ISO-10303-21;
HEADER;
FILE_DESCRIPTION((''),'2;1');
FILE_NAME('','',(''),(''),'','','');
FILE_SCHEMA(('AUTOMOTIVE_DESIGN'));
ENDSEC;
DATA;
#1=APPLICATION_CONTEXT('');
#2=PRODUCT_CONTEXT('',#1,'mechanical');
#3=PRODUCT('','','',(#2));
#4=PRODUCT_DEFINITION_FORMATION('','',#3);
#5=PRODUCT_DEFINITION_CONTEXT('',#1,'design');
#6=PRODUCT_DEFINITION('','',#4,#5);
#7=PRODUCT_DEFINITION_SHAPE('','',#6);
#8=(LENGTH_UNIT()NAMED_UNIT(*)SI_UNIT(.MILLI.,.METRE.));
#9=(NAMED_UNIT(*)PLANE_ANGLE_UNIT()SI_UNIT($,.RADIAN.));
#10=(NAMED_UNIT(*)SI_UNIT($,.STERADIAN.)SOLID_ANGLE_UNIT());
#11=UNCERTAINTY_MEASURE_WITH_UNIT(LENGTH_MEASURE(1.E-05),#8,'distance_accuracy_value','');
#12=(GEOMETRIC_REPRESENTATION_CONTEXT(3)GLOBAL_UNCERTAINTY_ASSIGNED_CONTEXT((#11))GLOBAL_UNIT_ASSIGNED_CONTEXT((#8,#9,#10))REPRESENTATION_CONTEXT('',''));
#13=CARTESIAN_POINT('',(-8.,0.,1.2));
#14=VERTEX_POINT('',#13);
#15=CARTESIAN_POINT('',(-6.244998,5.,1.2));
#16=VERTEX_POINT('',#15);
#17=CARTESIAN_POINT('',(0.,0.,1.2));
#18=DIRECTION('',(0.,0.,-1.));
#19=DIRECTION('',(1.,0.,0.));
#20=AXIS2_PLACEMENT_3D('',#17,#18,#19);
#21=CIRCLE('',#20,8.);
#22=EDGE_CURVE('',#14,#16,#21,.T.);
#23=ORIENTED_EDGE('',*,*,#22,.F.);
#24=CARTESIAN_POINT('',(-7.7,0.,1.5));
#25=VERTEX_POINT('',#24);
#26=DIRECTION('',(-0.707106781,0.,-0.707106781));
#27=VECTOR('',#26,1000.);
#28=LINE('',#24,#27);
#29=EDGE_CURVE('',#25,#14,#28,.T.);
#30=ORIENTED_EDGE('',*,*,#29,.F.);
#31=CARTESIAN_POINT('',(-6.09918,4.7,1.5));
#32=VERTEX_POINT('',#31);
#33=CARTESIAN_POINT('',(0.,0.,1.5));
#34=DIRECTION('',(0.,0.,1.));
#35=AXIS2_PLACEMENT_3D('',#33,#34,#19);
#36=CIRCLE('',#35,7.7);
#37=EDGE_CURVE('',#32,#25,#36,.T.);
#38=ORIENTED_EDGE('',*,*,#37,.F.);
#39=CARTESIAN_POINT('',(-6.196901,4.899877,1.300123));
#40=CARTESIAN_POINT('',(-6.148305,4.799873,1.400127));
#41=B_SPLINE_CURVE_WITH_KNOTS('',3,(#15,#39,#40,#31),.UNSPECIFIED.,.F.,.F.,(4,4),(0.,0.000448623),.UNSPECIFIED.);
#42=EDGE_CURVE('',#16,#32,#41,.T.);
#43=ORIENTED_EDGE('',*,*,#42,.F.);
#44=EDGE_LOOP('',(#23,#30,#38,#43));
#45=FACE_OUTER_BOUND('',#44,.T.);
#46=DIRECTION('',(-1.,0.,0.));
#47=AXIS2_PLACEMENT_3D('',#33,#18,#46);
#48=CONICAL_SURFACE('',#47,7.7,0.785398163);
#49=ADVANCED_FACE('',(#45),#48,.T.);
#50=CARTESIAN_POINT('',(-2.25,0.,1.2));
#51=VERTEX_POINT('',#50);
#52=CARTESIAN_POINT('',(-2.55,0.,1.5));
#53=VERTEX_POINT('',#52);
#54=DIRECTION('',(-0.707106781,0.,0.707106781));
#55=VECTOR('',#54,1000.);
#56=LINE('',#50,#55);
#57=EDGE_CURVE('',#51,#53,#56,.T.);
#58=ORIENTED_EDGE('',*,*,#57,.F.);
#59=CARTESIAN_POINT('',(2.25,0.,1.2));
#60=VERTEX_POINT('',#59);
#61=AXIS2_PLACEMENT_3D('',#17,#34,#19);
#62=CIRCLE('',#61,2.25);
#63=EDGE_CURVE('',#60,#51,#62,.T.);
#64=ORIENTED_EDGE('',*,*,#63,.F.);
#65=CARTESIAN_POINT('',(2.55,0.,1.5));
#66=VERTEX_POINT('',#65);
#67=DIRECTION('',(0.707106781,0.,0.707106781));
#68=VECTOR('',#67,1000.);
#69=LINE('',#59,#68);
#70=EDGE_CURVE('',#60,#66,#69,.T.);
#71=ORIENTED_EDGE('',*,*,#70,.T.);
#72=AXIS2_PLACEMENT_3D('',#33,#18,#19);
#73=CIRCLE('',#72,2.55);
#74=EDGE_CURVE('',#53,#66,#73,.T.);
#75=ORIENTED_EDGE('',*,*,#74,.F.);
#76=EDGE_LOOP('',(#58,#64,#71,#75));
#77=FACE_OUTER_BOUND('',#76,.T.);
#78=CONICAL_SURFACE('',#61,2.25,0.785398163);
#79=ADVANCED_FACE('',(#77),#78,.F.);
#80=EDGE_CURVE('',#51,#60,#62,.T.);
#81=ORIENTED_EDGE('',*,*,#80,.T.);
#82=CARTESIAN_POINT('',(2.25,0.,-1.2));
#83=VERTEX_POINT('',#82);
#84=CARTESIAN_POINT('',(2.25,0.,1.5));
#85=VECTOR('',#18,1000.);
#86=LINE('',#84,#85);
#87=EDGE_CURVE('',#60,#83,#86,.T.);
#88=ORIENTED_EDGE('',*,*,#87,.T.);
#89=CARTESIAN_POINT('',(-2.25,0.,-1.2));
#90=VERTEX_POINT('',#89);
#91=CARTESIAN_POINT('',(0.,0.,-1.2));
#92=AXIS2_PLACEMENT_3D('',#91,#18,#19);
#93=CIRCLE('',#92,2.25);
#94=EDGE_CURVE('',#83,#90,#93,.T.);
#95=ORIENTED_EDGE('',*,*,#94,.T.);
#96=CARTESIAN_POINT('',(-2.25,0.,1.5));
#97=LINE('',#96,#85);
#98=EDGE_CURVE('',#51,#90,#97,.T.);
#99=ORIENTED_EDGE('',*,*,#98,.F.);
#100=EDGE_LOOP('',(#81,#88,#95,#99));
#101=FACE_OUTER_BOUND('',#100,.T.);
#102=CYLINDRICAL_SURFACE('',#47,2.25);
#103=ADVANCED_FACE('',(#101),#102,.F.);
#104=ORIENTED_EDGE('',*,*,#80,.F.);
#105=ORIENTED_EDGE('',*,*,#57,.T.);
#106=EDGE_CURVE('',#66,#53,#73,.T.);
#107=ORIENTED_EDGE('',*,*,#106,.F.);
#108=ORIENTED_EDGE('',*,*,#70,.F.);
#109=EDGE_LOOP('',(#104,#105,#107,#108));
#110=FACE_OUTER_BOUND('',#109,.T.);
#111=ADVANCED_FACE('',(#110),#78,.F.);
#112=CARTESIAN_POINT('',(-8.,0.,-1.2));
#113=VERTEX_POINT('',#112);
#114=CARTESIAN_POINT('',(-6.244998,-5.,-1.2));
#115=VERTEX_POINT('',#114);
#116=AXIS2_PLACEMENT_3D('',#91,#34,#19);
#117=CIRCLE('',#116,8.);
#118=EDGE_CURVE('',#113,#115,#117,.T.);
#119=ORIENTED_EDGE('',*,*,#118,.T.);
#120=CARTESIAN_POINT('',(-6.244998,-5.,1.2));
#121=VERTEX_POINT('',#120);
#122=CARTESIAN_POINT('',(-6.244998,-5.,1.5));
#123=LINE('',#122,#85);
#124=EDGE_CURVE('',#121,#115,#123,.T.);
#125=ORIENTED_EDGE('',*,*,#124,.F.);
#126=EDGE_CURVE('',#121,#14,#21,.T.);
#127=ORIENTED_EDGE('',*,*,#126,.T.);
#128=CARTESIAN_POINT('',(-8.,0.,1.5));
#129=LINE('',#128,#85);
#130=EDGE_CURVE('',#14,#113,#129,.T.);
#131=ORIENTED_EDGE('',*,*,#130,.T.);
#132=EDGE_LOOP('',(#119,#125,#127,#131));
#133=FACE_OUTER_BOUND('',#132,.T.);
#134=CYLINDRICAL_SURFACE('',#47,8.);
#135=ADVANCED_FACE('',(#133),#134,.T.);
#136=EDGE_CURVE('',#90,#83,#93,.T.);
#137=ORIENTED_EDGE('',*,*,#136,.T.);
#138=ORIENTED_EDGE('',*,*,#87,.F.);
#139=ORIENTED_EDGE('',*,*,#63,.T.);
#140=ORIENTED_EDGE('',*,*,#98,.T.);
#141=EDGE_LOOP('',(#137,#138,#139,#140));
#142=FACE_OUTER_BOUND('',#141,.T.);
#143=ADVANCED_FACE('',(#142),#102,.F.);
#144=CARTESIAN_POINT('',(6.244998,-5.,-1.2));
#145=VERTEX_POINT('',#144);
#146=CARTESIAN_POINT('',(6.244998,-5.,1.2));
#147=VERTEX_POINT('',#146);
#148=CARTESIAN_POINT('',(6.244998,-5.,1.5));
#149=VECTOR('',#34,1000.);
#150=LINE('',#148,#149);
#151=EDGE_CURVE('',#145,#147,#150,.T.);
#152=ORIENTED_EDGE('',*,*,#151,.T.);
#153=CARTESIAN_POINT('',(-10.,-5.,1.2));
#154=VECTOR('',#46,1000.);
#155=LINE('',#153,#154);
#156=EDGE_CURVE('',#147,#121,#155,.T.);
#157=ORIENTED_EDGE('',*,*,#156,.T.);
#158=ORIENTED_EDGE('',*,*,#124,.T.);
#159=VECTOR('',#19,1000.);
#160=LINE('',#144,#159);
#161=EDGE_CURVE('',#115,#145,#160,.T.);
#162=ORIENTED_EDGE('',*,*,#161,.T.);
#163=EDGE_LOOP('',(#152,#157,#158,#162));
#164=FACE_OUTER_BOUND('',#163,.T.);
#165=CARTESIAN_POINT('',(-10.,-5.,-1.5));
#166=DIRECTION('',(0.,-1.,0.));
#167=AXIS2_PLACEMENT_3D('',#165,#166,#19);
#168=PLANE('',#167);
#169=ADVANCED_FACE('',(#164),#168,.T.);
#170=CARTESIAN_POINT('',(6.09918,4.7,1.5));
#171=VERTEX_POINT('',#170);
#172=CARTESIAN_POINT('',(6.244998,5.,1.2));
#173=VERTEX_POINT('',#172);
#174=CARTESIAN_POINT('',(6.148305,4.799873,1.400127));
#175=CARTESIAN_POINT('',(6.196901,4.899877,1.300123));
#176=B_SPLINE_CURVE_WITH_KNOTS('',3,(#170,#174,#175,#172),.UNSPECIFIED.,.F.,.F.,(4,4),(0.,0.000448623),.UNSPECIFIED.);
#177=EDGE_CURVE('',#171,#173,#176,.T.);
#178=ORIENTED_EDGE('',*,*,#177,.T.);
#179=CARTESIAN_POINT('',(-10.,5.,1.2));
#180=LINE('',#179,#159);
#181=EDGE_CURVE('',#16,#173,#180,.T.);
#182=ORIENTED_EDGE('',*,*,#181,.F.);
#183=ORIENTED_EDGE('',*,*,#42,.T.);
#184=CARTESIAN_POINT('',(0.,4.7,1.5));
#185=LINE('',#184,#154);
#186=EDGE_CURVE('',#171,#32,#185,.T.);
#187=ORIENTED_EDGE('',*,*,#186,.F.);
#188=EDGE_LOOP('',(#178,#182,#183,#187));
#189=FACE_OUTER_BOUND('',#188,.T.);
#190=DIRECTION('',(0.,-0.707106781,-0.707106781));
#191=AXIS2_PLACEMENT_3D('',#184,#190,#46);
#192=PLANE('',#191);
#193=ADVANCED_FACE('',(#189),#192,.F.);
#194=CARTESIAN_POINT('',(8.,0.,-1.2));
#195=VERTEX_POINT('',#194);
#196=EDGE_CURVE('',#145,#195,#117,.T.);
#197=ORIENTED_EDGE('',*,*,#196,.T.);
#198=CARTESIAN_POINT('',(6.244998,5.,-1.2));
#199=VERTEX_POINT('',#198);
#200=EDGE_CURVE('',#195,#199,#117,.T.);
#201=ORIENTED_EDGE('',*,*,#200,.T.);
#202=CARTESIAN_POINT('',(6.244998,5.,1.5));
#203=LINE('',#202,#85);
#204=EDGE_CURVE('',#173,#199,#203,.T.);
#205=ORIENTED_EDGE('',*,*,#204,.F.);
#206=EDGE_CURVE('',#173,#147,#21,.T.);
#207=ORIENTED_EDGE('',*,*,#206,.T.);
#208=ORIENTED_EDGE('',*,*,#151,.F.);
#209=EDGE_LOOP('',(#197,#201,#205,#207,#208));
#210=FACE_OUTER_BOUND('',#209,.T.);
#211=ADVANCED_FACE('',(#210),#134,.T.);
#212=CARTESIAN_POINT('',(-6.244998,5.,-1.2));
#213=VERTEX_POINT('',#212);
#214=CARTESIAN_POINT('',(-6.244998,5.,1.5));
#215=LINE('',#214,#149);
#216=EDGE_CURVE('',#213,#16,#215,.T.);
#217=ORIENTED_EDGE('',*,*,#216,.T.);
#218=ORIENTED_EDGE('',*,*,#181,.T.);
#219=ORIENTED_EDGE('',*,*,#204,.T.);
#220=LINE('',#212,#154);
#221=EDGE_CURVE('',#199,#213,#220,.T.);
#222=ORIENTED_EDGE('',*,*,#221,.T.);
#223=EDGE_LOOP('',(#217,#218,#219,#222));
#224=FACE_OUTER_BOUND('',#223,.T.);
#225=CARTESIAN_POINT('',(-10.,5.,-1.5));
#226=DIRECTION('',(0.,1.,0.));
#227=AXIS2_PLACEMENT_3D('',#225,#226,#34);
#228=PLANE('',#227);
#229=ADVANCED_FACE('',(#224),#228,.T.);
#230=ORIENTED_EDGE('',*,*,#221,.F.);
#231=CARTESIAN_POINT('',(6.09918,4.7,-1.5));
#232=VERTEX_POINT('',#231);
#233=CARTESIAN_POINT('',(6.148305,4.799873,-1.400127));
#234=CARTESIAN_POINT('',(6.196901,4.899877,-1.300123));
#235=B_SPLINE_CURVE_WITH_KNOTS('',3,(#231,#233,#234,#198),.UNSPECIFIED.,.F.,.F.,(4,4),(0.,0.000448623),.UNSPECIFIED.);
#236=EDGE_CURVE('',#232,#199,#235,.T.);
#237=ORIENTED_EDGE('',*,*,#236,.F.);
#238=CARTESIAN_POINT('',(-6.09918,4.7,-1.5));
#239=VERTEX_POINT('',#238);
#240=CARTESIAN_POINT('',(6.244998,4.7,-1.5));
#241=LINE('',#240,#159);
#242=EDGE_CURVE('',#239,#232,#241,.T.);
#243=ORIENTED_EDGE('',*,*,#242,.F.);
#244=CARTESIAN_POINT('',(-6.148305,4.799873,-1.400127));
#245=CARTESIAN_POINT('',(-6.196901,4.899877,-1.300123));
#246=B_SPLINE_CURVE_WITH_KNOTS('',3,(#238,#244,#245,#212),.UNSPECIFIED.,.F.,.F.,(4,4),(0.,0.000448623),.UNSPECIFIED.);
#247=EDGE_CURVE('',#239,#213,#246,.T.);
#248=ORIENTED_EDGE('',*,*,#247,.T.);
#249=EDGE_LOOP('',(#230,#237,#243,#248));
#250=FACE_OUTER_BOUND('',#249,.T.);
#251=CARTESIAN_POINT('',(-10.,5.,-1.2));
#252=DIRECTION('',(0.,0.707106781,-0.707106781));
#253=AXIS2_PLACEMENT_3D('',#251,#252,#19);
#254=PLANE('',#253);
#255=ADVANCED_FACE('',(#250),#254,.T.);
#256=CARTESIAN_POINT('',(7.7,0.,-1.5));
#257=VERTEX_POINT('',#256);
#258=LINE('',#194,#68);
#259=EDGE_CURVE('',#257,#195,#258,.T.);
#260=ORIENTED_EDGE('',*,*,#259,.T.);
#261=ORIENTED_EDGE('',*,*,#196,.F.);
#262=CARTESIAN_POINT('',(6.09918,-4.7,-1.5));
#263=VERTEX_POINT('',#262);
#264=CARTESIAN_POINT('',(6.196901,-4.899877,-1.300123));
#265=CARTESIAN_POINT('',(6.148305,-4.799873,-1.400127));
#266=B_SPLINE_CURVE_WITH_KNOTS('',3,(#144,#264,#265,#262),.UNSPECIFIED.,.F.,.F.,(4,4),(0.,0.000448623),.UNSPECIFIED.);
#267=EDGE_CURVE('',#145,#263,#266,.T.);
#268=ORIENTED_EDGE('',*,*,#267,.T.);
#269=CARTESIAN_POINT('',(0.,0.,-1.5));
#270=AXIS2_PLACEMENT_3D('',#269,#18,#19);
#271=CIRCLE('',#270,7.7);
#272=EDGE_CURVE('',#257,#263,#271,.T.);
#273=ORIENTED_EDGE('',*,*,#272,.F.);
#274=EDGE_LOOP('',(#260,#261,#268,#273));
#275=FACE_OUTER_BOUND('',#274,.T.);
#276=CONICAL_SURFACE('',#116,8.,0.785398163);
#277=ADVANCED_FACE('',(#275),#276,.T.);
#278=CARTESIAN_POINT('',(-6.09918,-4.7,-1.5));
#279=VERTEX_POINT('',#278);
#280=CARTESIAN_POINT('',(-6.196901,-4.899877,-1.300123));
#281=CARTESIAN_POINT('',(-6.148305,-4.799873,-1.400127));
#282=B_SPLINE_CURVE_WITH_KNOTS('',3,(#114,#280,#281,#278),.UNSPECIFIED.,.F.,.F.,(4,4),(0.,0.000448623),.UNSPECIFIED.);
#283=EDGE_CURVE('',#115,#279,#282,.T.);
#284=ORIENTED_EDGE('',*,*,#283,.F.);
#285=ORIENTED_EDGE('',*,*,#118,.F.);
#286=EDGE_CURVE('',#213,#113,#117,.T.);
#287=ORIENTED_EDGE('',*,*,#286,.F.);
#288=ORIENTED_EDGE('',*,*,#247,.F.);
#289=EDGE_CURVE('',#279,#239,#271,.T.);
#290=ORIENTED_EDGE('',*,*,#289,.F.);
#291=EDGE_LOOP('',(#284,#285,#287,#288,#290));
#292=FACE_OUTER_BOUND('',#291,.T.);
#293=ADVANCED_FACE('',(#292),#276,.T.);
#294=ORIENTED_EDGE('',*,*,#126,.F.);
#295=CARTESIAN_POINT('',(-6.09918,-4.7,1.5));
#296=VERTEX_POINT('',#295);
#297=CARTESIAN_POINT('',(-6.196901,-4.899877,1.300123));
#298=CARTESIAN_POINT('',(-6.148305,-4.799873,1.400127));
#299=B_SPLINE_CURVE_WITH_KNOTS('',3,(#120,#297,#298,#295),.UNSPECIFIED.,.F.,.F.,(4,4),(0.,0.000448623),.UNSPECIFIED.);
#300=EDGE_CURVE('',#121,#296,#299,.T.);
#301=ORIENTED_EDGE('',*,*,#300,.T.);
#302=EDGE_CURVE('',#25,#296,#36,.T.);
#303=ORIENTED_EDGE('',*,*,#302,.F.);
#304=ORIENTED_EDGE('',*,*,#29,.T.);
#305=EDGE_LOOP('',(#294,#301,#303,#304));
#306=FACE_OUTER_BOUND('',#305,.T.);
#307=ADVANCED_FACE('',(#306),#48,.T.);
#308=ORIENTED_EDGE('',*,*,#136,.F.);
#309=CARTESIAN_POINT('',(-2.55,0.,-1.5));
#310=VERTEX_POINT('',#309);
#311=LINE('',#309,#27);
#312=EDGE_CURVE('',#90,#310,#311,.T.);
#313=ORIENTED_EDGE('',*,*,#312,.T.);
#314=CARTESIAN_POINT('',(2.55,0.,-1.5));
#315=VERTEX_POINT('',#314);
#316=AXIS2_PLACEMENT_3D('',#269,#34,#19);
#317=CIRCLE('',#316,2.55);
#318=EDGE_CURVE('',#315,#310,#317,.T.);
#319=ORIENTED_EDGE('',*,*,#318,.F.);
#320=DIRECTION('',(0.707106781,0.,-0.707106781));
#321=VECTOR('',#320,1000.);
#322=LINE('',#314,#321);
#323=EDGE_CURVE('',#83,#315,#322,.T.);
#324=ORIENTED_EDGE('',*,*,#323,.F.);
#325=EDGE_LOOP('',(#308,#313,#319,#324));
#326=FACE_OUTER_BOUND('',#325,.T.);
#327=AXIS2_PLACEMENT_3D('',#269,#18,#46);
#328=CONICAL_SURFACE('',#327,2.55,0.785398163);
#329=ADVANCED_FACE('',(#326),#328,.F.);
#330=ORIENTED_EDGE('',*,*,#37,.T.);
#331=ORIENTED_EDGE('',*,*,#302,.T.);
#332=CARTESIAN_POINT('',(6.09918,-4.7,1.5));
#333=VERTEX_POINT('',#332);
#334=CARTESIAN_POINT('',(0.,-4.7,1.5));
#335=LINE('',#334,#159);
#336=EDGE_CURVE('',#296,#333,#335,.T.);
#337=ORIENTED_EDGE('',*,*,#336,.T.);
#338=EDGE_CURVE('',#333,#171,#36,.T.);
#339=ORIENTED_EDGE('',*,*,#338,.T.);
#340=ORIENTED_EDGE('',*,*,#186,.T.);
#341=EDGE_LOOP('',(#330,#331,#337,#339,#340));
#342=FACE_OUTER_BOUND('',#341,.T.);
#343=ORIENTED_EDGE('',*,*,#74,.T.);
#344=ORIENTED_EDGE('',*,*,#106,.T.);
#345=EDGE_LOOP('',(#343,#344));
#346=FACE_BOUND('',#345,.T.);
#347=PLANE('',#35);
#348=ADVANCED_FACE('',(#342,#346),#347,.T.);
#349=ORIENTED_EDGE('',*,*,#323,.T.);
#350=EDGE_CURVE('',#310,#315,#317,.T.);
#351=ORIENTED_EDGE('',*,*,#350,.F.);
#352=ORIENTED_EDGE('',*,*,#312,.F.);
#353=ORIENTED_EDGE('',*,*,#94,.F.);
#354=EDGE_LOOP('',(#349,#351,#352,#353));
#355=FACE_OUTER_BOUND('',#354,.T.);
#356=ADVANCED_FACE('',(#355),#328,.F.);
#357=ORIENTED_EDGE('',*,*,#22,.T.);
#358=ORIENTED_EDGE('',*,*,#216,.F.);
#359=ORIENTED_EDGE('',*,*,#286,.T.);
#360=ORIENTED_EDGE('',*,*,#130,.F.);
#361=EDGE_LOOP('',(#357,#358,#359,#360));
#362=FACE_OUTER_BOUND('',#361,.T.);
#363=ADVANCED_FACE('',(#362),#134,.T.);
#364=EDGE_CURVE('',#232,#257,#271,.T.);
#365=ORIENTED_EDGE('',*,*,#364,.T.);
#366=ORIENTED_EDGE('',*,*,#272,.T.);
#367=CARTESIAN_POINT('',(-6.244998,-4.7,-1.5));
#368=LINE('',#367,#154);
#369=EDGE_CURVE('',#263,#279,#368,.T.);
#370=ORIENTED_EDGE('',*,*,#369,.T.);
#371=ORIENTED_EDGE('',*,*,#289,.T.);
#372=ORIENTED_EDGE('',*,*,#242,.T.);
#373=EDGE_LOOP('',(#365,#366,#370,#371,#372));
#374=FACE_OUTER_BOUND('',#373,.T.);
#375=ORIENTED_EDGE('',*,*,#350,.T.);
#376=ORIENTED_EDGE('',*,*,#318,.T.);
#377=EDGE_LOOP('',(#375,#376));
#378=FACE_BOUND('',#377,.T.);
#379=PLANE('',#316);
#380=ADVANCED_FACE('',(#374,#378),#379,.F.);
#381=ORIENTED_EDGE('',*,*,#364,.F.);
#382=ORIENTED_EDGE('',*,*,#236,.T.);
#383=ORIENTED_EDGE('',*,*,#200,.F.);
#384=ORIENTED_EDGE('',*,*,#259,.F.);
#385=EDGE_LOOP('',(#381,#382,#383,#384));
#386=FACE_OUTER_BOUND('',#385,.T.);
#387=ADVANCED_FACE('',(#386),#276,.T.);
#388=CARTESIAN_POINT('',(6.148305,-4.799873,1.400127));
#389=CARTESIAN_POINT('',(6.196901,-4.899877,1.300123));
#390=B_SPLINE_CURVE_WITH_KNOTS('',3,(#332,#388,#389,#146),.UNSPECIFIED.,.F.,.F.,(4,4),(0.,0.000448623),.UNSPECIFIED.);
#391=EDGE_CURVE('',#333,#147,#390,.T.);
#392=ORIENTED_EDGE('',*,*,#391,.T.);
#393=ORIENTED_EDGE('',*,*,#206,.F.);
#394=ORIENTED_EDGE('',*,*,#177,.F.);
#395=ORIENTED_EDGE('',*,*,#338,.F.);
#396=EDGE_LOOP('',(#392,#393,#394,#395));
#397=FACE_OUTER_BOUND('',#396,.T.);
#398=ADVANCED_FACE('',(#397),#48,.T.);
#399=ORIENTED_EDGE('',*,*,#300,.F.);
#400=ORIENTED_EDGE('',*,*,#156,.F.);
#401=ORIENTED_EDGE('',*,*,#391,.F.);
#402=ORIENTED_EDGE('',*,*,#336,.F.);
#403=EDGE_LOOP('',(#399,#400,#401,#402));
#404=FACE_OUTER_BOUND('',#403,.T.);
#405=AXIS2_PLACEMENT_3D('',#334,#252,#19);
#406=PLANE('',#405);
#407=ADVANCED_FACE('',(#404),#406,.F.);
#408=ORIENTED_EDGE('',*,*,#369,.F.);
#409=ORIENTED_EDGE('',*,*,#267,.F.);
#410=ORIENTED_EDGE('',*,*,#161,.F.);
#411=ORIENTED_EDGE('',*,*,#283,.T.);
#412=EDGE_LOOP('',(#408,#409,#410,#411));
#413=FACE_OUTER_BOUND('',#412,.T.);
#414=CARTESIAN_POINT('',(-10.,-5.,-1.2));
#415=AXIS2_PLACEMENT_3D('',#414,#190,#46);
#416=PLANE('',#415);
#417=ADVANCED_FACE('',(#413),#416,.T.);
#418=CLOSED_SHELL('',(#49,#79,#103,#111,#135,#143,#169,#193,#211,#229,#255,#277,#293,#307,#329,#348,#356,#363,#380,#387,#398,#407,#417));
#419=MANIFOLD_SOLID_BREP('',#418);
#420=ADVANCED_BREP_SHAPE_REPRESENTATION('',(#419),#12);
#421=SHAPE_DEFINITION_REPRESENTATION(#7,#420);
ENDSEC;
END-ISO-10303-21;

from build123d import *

# Parameters (mm, degrees)
SKETCH1_R           = 8
SKETCH1_R_2         = 2.25
BOSS_EXTRUDE1_DEPTH = 1.5
SKETCH2_OUTSIDE_W   = 22.566
SKETCH2_OUTSIDE_H   = 22.566
SKETCH2_OUTSIDE_W_2 = 20
SKETCH2_OUTSIDE_H_2 = 10
CUT_EXTRUDE1_DEPTH  = 12.704699911
CHAMFER1_SIZE       = 0.3


with BuildPart() as part:
    # Sketch1 → Boss-Extrude1 (new, symmetric)
    with BuildSketch(Plane.XY):
        Circle(SKETCH1_R)
        Circle(SKETCH1_R_2, mode=Mode.SUBTRACT)
    extrude(amount=BOSS_EXTRUDE1_DEPTH, both=True)

    # Sketch2 outside → Cut-Extrude1 (cut, through all)
    with BuildSketch(Plane.XY.offset(1.5)):
        Rectangle(SKETCH2_OUTSIDE_W, SKETCH2_OUTSIDE_H)
        Rectangle(SKETCH2_OUTSIDE_W_2, SKETCH2_OUTSIDE_H_2, mode=Mode.SUBTRACT)
    extrude(amount=-CUT_EXTRUDE1_DEPTH, mode=Mode.SUBTRACT)

    # Chamfer1
    chamfer1_edges = [part.edges().sort_by_distance(p)[0] for p in [
        (8, 0, 1.5),
        (-8, 0, -1.5),
        (8, 0, -1.5),
        (0, 5, -1.5),
        (0, -5, -1.5),
        (0, -5, 1.5),
        (0, 5, 1.5),
        (-2.25, 0, -1.5),
        (-2.25, 0, 1.5),
        (-8, 0, 1.5),
    ]]
    chamfer(chamfer1_edges, length=CHAMFER1_SIZE)


solid = part.part
